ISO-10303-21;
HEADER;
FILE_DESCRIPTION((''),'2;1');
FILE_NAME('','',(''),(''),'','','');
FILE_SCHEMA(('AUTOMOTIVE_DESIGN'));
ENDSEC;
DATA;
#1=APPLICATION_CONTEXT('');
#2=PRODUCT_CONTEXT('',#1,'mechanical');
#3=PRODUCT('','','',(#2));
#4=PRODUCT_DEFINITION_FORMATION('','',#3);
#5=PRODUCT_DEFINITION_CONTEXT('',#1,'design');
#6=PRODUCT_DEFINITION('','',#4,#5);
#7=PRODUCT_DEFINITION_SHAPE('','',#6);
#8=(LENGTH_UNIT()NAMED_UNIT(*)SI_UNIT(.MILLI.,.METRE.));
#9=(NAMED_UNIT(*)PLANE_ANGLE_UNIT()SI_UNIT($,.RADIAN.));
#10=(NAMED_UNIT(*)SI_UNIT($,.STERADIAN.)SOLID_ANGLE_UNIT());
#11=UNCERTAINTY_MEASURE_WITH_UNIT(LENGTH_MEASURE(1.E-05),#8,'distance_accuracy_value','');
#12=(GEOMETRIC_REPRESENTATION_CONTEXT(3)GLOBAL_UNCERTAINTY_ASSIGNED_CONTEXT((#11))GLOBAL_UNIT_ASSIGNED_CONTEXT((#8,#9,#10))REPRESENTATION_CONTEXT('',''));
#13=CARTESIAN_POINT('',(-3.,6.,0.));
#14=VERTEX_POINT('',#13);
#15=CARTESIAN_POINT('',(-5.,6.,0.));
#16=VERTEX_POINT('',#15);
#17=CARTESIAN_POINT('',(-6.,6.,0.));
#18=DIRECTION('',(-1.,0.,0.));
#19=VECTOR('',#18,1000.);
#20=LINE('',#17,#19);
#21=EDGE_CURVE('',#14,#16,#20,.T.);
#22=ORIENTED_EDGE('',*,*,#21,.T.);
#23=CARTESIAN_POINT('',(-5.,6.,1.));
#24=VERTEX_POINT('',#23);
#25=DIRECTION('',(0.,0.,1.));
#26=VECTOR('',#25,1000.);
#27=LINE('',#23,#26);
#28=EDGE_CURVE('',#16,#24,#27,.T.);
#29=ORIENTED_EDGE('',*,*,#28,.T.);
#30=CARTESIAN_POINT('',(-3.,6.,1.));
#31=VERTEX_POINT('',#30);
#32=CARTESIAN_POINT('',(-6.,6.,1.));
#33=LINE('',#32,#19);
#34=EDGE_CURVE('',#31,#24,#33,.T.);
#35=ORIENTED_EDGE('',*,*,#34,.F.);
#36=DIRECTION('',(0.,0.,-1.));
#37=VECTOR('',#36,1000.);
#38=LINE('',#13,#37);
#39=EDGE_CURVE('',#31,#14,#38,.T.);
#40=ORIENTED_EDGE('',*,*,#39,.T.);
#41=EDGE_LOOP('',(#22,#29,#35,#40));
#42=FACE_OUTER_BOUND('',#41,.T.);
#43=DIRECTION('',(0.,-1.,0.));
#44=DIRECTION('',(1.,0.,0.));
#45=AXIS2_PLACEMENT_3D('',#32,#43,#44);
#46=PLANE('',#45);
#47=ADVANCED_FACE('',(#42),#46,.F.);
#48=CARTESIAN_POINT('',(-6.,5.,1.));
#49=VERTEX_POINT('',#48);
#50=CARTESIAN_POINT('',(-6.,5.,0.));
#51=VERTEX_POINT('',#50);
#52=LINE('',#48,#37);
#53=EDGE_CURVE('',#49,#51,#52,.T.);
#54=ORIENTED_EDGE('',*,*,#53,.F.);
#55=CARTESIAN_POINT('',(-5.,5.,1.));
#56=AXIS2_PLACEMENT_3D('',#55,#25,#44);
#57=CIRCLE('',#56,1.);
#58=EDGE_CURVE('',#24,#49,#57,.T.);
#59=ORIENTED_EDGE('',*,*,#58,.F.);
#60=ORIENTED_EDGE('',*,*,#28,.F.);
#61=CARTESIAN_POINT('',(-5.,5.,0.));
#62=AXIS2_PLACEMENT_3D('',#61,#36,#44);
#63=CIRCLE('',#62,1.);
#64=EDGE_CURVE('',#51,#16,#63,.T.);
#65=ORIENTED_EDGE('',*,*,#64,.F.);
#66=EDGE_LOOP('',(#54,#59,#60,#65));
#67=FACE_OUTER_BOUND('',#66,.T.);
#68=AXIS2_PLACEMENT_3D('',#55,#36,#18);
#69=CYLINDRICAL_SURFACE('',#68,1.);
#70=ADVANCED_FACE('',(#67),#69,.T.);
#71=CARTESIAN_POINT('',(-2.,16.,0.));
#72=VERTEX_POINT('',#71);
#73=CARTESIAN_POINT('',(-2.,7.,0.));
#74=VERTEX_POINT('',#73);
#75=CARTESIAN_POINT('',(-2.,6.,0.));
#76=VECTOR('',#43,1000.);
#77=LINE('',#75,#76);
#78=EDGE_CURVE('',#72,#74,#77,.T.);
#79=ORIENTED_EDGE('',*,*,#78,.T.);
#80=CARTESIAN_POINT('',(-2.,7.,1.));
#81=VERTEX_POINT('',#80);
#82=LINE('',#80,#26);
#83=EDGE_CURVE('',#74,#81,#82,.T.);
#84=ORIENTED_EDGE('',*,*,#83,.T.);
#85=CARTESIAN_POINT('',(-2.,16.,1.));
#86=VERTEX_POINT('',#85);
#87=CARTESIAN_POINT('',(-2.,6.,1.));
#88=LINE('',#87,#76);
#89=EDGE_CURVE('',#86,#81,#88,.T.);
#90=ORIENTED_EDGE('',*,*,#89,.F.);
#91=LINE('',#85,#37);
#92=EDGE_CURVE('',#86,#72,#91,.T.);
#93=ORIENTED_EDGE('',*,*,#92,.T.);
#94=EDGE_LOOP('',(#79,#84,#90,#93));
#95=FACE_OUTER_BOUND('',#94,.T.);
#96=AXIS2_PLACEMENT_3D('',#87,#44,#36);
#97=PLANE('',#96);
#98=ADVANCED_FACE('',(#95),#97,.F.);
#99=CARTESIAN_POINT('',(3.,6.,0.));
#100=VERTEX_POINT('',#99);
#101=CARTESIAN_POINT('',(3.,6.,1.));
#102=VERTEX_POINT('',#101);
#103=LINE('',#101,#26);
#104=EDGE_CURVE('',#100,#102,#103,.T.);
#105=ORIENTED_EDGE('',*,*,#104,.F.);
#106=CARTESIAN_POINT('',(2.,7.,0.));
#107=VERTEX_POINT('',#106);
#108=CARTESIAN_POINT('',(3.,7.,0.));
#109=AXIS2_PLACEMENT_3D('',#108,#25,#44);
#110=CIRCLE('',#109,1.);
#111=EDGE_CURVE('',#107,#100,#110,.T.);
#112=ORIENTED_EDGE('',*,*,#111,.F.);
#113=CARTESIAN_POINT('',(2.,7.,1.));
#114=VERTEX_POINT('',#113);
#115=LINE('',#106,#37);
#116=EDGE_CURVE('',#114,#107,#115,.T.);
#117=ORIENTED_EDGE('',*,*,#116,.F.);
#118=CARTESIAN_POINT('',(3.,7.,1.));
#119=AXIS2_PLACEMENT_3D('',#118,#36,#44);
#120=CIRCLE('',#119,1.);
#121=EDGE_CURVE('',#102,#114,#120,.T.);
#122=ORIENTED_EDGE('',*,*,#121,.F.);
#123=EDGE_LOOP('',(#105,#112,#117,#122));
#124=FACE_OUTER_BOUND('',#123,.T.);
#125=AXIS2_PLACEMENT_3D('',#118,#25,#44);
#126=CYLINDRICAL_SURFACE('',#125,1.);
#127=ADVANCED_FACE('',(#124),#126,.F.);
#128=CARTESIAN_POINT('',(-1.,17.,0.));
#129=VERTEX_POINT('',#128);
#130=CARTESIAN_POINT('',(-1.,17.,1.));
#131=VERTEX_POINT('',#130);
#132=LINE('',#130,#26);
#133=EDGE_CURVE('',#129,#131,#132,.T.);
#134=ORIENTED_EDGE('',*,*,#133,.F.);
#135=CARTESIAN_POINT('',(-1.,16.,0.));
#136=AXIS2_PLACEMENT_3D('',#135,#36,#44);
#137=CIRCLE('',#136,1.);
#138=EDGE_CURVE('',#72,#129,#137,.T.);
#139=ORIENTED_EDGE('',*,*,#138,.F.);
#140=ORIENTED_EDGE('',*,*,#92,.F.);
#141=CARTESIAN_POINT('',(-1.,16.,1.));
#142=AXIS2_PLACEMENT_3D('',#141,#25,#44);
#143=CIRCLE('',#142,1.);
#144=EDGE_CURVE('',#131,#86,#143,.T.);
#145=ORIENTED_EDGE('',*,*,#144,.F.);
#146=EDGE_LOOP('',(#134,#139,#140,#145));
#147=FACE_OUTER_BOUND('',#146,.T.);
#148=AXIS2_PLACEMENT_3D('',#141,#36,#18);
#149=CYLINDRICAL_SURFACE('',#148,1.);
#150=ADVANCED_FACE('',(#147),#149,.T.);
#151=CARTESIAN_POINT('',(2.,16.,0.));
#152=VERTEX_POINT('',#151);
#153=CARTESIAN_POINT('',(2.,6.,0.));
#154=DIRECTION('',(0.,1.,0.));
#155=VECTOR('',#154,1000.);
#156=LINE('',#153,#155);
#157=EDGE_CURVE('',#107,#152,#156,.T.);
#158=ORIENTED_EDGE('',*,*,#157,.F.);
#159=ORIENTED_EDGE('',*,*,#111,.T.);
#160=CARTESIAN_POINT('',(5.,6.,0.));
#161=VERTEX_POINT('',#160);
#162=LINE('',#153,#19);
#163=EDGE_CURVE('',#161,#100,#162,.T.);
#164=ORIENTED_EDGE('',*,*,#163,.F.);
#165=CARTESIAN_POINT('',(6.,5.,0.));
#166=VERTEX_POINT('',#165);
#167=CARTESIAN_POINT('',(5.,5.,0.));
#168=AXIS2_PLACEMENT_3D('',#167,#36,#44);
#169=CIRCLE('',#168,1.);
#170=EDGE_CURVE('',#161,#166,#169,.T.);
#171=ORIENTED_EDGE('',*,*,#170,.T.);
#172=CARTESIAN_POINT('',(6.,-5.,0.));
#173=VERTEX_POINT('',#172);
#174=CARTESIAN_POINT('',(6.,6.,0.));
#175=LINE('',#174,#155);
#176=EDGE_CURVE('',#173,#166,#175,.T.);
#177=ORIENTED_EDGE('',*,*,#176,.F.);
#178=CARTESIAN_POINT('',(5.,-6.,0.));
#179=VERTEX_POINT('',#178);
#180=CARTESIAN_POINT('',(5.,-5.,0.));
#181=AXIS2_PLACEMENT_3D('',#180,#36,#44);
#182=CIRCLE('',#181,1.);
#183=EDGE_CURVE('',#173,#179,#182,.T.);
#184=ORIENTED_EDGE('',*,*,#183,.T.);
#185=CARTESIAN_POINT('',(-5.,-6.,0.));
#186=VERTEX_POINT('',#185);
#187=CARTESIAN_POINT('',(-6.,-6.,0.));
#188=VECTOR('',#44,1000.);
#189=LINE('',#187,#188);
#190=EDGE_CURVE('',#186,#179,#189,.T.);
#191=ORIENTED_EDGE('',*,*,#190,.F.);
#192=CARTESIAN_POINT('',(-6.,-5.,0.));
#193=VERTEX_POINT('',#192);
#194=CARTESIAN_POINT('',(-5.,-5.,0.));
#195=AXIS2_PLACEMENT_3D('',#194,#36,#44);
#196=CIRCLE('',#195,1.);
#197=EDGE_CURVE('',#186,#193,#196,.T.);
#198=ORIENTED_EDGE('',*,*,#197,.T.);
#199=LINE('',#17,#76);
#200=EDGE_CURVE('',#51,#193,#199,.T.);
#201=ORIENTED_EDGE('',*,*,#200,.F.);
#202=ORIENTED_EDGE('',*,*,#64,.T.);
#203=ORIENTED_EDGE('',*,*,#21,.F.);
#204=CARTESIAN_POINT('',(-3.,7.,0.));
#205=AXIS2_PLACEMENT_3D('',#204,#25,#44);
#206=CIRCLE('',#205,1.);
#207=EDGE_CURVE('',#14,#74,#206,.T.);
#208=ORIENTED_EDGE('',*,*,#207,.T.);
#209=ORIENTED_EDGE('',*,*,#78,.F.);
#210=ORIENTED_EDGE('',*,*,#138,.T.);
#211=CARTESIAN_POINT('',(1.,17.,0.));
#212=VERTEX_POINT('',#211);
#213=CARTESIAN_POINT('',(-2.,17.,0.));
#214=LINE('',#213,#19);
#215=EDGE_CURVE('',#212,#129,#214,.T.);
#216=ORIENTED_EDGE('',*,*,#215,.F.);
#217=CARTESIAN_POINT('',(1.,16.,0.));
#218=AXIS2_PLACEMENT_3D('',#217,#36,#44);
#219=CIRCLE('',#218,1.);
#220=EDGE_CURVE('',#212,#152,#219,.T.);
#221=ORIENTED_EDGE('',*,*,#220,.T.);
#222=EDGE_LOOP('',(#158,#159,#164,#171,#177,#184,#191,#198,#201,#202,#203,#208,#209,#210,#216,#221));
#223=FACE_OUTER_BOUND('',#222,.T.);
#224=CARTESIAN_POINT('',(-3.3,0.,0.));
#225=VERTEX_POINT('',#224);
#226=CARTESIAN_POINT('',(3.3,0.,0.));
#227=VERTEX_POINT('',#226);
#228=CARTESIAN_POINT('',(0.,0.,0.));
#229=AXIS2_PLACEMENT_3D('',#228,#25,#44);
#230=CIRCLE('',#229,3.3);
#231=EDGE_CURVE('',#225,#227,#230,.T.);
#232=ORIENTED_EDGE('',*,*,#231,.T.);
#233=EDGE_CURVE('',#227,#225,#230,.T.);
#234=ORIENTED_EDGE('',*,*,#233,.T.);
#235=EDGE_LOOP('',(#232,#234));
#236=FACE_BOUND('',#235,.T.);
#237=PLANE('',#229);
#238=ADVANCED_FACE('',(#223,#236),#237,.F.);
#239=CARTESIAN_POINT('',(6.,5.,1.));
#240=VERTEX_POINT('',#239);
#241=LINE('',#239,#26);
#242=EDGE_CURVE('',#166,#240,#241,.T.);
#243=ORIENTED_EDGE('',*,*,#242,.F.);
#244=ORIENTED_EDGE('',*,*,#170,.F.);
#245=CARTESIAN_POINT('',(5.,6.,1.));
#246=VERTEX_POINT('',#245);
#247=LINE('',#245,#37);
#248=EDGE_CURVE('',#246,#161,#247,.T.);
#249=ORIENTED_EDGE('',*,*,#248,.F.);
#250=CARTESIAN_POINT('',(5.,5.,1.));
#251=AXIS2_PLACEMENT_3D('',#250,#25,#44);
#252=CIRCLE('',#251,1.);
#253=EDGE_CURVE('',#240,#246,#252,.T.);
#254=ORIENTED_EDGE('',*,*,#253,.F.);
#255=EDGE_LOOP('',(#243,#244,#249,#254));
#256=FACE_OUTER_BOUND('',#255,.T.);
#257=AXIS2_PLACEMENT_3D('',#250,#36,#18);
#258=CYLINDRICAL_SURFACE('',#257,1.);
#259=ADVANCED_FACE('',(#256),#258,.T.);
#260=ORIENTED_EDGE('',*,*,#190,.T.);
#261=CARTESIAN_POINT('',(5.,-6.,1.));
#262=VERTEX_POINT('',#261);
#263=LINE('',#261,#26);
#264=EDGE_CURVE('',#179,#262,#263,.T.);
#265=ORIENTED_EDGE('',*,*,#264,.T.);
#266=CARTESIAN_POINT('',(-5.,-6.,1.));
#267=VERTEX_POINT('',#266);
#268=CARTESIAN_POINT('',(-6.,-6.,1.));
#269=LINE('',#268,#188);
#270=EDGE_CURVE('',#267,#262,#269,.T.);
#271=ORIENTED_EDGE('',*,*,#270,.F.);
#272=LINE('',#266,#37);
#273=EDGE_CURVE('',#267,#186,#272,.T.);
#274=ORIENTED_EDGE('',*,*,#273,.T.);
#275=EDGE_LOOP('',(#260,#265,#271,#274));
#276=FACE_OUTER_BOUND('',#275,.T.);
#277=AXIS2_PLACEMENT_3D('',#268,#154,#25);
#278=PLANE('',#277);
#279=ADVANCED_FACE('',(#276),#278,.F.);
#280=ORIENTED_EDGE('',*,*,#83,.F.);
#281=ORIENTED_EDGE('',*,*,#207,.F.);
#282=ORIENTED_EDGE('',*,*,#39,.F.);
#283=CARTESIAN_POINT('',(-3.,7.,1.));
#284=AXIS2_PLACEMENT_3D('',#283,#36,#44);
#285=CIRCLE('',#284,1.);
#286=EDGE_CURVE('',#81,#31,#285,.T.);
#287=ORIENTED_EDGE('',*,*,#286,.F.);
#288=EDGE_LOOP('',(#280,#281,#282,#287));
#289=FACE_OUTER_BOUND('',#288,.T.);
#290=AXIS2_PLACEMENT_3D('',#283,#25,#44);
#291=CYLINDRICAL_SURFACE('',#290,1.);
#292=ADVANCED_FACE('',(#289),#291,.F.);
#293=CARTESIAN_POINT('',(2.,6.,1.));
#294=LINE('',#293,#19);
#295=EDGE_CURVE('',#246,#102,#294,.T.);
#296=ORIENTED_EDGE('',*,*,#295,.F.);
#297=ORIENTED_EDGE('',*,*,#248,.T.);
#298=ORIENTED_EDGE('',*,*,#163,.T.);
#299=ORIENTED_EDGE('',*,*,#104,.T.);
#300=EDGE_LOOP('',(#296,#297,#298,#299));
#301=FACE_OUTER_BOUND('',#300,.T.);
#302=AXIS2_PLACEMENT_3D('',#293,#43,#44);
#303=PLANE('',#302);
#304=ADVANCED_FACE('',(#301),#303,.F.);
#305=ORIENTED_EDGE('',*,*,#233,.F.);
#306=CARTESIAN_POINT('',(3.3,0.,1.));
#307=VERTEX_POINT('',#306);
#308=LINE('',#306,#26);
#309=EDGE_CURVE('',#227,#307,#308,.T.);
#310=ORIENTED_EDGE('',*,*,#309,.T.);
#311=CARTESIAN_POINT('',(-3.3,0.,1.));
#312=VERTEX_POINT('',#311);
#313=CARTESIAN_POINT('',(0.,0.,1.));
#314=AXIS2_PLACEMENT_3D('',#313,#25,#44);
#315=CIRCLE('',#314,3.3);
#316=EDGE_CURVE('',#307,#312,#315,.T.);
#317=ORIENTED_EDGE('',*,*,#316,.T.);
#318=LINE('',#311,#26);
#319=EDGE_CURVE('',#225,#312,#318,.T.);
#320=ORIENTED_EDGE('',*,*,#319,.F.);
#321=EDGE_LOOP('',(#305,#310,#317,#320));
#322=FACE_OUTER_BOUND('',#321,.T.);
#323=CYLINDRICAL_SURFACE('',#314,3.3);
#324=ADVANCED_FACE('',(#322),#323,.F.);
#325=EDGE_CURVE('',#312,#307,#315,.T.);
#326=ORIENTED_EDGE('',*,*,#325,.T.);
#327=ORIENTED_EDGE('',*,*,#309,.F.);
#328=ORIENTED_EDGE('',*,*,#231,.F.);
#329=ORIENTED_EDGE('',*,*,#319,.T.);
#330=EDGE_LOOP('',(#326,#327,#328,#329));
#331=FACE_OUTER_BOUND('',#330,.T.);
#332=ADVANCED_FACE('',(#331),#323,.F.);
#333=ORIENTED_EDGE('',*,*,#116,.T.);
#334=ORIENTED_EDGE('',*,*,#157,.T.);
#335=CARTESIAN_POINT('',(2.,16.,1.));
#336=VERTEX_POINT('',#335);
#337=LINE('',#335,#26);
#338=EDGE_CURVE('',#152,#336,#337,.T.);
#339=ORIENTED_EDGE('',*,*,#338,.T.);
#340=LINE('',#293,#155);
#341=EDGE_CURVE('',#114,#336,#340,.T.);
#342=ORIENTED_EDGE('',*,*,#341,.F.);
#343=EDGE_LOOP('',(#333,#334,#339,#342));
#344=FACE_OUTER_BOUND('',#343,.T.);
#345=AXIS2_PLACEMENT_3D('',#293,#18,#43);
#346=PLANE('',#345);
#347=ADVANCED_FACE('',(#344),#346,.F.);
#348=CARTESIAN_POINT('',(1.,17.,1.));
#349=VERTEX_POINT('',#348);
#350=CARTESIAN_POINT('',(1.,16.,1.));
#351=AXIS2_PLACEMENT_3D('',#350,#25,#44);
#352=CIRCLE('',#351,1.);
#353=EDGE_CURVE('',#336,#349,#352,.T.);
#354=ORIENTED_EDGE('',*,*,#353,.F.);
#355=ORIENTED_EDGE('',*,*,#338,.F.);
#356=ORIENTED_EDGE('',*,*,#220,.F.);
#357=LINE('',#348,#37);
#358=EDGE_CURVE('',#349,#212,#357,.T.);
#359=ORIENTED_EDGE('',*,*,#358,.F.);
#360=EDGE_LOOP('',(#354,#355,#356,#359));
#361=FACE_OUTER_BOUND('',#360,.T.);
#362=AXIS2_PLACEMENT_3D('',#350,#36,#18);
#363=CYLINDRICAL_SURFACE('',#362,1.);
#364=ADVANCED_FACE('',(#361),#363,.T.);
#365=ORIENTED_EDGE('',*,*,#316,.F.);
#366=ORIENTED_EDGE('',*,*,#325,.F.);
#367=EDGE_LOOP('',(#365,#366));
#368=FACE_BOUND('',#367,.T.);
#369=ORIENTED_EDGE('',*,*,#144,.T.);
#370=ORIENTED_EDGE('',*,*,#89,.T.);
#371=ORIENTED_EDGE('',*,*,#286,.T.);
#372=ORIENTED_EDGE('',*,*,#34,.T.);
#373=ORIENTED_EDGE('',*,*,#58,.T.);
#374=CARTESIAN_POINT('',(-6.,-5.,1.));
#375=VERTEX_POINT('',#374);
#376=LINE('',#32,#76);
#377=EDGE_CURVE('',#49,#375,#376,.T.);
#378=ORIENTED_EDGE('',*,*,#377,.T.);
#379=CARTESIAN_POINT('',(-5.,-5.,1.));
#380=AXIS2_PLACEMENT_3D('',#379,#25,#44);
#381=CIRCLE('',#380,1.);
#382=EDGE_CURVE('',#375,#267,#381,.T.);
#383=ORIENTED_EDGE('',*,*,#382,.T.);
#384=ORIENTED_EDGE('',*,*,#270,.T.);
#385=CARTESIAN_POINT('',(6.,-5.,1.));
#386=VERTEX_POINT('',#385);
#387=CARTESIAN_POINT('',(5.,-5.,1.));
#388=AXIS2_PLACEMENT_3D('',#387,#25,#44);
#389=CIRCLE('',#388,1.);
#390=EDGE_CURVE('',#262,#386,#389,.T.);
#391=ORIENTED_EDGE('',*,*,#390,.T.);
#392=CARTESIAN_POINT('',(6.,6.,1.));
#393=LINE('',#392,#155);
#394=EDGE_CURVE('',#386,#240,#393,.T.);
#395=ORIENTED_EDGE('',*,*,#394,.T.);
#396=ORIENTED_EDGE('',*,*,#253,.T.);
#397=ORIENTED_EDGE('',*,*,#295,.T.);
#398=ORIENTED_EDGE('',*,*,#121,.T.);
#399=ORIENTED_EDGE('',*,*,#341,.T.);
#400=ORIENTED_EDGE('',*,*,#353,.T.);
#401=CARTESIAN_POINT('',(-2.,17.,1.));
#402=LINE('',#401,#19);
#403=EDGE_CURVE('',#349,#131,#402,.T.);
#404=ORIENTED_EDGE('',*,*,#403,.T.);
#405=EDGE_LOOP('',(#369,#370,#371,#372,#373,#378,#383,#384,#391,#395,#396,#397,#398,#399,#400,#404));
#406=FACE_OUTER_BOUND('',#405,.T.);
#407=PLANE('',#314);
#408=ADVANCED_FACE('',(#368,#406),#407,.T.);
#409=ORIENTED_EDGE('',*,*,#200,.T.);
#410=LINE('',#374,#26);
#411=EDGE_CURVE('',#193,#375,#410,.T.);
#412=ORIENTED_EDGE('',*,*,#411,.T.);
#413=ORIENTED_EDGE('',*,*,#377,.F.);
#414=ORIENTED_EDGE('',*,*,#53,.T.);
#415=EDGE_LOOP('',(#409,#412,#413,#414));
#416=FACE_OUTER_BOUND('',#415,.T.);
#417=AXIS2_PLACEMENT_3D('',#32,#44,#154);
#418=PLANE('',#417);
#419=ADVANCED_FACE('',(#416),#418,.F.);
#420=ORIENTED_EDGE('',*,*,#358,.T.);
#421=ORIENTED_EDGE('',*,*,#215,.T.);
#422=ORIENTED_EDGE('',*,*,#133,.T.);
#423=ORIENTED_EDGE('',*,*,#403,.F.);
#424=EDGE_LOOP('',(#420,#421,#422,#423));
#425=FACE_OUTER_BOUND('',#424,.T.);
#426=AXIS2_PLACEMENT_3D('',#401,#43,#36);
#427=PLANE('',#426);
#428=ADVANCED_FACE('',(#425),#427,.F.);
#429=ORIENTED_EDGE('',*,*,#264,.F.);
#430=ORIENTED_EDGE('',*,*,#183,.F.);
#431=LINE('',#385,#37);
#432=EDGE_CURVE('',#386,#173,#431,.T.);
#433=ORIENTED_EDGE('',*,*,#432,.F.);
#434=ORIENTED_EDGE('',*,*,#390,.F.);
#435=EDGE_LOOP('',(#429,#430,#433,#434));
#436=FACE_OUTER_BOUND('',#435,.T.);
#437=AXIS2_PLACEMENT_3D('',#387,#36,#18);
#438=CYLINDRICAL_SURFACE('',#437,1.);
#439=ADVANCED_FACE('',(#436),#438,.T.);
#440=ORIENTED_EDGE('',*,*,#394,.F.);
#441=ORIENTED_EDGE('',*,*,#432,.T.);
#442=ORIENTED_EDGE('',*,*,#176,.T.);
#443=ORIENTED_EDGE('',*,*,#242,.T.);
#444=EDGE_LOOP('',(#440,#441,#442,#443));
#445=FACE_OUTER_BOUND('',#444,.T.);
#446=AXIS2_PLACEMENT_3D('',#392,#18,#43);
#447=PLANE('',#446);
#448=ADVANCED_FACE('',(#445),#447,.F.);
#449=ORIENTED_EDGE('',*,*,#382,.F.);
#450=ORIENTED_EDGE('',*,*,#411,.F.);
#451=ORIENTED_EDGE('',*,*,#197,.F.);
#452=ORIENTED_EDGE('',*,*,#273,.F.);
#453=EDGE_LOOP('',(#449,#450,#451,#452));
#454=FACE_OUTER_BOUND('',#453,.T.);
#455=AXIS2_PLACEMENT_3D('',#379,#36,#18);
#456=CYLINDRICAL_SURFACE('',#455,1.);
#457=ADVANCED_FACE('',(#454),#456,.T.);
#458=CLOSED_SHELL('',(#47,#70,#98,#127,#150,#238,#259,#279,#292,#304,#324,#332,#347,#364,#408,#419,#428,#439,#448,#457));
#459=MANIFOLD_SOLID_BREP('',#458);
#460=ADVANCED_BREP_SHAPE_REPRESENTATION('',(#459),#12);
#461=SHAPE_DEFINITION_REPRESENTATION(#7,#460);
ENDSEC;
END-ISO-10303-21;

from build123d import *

# Parameters (mm, degrees)
BOSS_EXTRUDE1_DEPTH  = 1
M6_CLEARANCE_HOLE1_D = 6.6
FILLET1_R            = 1


with BuildPart() as part:
    # Sketch1 → Boss-Extrude1 (new body)
    with BuildSketch(Plane.XY):
        Polygon((2, 6), (6, 6), (6, -6), (-6, -6), (-6, 6), (-2, 6), (-2, 17), (2, 17), align=None)
    extrude(amount=BOSS_EXTRUDE1_DEPTH)

    # M6 Clearance Hole1 (through all)
    with Locations(Plane.XY.offset(1)):
        with Locations((0, 0)):
            Hole(M6_CLEARANCE_HOLE1_D / 2)

    # Fillet1
    fillet1_edges = [part.edges().sort_by_distance(p)[0] for p in [
        (6, -6, 0.5),
        (-6, -6, 0.5),
        (-6, 6, 0.5),
        (-2, 6, 0.5),
        (-2, 17, 0.5),
        (2, 17, 0.5),
        (2, 6, 0.5),
        (6, 6, 0.5),
    ]]
    fillet(fillet1_edges, radius=FILLET1_R)


solid = part.part
